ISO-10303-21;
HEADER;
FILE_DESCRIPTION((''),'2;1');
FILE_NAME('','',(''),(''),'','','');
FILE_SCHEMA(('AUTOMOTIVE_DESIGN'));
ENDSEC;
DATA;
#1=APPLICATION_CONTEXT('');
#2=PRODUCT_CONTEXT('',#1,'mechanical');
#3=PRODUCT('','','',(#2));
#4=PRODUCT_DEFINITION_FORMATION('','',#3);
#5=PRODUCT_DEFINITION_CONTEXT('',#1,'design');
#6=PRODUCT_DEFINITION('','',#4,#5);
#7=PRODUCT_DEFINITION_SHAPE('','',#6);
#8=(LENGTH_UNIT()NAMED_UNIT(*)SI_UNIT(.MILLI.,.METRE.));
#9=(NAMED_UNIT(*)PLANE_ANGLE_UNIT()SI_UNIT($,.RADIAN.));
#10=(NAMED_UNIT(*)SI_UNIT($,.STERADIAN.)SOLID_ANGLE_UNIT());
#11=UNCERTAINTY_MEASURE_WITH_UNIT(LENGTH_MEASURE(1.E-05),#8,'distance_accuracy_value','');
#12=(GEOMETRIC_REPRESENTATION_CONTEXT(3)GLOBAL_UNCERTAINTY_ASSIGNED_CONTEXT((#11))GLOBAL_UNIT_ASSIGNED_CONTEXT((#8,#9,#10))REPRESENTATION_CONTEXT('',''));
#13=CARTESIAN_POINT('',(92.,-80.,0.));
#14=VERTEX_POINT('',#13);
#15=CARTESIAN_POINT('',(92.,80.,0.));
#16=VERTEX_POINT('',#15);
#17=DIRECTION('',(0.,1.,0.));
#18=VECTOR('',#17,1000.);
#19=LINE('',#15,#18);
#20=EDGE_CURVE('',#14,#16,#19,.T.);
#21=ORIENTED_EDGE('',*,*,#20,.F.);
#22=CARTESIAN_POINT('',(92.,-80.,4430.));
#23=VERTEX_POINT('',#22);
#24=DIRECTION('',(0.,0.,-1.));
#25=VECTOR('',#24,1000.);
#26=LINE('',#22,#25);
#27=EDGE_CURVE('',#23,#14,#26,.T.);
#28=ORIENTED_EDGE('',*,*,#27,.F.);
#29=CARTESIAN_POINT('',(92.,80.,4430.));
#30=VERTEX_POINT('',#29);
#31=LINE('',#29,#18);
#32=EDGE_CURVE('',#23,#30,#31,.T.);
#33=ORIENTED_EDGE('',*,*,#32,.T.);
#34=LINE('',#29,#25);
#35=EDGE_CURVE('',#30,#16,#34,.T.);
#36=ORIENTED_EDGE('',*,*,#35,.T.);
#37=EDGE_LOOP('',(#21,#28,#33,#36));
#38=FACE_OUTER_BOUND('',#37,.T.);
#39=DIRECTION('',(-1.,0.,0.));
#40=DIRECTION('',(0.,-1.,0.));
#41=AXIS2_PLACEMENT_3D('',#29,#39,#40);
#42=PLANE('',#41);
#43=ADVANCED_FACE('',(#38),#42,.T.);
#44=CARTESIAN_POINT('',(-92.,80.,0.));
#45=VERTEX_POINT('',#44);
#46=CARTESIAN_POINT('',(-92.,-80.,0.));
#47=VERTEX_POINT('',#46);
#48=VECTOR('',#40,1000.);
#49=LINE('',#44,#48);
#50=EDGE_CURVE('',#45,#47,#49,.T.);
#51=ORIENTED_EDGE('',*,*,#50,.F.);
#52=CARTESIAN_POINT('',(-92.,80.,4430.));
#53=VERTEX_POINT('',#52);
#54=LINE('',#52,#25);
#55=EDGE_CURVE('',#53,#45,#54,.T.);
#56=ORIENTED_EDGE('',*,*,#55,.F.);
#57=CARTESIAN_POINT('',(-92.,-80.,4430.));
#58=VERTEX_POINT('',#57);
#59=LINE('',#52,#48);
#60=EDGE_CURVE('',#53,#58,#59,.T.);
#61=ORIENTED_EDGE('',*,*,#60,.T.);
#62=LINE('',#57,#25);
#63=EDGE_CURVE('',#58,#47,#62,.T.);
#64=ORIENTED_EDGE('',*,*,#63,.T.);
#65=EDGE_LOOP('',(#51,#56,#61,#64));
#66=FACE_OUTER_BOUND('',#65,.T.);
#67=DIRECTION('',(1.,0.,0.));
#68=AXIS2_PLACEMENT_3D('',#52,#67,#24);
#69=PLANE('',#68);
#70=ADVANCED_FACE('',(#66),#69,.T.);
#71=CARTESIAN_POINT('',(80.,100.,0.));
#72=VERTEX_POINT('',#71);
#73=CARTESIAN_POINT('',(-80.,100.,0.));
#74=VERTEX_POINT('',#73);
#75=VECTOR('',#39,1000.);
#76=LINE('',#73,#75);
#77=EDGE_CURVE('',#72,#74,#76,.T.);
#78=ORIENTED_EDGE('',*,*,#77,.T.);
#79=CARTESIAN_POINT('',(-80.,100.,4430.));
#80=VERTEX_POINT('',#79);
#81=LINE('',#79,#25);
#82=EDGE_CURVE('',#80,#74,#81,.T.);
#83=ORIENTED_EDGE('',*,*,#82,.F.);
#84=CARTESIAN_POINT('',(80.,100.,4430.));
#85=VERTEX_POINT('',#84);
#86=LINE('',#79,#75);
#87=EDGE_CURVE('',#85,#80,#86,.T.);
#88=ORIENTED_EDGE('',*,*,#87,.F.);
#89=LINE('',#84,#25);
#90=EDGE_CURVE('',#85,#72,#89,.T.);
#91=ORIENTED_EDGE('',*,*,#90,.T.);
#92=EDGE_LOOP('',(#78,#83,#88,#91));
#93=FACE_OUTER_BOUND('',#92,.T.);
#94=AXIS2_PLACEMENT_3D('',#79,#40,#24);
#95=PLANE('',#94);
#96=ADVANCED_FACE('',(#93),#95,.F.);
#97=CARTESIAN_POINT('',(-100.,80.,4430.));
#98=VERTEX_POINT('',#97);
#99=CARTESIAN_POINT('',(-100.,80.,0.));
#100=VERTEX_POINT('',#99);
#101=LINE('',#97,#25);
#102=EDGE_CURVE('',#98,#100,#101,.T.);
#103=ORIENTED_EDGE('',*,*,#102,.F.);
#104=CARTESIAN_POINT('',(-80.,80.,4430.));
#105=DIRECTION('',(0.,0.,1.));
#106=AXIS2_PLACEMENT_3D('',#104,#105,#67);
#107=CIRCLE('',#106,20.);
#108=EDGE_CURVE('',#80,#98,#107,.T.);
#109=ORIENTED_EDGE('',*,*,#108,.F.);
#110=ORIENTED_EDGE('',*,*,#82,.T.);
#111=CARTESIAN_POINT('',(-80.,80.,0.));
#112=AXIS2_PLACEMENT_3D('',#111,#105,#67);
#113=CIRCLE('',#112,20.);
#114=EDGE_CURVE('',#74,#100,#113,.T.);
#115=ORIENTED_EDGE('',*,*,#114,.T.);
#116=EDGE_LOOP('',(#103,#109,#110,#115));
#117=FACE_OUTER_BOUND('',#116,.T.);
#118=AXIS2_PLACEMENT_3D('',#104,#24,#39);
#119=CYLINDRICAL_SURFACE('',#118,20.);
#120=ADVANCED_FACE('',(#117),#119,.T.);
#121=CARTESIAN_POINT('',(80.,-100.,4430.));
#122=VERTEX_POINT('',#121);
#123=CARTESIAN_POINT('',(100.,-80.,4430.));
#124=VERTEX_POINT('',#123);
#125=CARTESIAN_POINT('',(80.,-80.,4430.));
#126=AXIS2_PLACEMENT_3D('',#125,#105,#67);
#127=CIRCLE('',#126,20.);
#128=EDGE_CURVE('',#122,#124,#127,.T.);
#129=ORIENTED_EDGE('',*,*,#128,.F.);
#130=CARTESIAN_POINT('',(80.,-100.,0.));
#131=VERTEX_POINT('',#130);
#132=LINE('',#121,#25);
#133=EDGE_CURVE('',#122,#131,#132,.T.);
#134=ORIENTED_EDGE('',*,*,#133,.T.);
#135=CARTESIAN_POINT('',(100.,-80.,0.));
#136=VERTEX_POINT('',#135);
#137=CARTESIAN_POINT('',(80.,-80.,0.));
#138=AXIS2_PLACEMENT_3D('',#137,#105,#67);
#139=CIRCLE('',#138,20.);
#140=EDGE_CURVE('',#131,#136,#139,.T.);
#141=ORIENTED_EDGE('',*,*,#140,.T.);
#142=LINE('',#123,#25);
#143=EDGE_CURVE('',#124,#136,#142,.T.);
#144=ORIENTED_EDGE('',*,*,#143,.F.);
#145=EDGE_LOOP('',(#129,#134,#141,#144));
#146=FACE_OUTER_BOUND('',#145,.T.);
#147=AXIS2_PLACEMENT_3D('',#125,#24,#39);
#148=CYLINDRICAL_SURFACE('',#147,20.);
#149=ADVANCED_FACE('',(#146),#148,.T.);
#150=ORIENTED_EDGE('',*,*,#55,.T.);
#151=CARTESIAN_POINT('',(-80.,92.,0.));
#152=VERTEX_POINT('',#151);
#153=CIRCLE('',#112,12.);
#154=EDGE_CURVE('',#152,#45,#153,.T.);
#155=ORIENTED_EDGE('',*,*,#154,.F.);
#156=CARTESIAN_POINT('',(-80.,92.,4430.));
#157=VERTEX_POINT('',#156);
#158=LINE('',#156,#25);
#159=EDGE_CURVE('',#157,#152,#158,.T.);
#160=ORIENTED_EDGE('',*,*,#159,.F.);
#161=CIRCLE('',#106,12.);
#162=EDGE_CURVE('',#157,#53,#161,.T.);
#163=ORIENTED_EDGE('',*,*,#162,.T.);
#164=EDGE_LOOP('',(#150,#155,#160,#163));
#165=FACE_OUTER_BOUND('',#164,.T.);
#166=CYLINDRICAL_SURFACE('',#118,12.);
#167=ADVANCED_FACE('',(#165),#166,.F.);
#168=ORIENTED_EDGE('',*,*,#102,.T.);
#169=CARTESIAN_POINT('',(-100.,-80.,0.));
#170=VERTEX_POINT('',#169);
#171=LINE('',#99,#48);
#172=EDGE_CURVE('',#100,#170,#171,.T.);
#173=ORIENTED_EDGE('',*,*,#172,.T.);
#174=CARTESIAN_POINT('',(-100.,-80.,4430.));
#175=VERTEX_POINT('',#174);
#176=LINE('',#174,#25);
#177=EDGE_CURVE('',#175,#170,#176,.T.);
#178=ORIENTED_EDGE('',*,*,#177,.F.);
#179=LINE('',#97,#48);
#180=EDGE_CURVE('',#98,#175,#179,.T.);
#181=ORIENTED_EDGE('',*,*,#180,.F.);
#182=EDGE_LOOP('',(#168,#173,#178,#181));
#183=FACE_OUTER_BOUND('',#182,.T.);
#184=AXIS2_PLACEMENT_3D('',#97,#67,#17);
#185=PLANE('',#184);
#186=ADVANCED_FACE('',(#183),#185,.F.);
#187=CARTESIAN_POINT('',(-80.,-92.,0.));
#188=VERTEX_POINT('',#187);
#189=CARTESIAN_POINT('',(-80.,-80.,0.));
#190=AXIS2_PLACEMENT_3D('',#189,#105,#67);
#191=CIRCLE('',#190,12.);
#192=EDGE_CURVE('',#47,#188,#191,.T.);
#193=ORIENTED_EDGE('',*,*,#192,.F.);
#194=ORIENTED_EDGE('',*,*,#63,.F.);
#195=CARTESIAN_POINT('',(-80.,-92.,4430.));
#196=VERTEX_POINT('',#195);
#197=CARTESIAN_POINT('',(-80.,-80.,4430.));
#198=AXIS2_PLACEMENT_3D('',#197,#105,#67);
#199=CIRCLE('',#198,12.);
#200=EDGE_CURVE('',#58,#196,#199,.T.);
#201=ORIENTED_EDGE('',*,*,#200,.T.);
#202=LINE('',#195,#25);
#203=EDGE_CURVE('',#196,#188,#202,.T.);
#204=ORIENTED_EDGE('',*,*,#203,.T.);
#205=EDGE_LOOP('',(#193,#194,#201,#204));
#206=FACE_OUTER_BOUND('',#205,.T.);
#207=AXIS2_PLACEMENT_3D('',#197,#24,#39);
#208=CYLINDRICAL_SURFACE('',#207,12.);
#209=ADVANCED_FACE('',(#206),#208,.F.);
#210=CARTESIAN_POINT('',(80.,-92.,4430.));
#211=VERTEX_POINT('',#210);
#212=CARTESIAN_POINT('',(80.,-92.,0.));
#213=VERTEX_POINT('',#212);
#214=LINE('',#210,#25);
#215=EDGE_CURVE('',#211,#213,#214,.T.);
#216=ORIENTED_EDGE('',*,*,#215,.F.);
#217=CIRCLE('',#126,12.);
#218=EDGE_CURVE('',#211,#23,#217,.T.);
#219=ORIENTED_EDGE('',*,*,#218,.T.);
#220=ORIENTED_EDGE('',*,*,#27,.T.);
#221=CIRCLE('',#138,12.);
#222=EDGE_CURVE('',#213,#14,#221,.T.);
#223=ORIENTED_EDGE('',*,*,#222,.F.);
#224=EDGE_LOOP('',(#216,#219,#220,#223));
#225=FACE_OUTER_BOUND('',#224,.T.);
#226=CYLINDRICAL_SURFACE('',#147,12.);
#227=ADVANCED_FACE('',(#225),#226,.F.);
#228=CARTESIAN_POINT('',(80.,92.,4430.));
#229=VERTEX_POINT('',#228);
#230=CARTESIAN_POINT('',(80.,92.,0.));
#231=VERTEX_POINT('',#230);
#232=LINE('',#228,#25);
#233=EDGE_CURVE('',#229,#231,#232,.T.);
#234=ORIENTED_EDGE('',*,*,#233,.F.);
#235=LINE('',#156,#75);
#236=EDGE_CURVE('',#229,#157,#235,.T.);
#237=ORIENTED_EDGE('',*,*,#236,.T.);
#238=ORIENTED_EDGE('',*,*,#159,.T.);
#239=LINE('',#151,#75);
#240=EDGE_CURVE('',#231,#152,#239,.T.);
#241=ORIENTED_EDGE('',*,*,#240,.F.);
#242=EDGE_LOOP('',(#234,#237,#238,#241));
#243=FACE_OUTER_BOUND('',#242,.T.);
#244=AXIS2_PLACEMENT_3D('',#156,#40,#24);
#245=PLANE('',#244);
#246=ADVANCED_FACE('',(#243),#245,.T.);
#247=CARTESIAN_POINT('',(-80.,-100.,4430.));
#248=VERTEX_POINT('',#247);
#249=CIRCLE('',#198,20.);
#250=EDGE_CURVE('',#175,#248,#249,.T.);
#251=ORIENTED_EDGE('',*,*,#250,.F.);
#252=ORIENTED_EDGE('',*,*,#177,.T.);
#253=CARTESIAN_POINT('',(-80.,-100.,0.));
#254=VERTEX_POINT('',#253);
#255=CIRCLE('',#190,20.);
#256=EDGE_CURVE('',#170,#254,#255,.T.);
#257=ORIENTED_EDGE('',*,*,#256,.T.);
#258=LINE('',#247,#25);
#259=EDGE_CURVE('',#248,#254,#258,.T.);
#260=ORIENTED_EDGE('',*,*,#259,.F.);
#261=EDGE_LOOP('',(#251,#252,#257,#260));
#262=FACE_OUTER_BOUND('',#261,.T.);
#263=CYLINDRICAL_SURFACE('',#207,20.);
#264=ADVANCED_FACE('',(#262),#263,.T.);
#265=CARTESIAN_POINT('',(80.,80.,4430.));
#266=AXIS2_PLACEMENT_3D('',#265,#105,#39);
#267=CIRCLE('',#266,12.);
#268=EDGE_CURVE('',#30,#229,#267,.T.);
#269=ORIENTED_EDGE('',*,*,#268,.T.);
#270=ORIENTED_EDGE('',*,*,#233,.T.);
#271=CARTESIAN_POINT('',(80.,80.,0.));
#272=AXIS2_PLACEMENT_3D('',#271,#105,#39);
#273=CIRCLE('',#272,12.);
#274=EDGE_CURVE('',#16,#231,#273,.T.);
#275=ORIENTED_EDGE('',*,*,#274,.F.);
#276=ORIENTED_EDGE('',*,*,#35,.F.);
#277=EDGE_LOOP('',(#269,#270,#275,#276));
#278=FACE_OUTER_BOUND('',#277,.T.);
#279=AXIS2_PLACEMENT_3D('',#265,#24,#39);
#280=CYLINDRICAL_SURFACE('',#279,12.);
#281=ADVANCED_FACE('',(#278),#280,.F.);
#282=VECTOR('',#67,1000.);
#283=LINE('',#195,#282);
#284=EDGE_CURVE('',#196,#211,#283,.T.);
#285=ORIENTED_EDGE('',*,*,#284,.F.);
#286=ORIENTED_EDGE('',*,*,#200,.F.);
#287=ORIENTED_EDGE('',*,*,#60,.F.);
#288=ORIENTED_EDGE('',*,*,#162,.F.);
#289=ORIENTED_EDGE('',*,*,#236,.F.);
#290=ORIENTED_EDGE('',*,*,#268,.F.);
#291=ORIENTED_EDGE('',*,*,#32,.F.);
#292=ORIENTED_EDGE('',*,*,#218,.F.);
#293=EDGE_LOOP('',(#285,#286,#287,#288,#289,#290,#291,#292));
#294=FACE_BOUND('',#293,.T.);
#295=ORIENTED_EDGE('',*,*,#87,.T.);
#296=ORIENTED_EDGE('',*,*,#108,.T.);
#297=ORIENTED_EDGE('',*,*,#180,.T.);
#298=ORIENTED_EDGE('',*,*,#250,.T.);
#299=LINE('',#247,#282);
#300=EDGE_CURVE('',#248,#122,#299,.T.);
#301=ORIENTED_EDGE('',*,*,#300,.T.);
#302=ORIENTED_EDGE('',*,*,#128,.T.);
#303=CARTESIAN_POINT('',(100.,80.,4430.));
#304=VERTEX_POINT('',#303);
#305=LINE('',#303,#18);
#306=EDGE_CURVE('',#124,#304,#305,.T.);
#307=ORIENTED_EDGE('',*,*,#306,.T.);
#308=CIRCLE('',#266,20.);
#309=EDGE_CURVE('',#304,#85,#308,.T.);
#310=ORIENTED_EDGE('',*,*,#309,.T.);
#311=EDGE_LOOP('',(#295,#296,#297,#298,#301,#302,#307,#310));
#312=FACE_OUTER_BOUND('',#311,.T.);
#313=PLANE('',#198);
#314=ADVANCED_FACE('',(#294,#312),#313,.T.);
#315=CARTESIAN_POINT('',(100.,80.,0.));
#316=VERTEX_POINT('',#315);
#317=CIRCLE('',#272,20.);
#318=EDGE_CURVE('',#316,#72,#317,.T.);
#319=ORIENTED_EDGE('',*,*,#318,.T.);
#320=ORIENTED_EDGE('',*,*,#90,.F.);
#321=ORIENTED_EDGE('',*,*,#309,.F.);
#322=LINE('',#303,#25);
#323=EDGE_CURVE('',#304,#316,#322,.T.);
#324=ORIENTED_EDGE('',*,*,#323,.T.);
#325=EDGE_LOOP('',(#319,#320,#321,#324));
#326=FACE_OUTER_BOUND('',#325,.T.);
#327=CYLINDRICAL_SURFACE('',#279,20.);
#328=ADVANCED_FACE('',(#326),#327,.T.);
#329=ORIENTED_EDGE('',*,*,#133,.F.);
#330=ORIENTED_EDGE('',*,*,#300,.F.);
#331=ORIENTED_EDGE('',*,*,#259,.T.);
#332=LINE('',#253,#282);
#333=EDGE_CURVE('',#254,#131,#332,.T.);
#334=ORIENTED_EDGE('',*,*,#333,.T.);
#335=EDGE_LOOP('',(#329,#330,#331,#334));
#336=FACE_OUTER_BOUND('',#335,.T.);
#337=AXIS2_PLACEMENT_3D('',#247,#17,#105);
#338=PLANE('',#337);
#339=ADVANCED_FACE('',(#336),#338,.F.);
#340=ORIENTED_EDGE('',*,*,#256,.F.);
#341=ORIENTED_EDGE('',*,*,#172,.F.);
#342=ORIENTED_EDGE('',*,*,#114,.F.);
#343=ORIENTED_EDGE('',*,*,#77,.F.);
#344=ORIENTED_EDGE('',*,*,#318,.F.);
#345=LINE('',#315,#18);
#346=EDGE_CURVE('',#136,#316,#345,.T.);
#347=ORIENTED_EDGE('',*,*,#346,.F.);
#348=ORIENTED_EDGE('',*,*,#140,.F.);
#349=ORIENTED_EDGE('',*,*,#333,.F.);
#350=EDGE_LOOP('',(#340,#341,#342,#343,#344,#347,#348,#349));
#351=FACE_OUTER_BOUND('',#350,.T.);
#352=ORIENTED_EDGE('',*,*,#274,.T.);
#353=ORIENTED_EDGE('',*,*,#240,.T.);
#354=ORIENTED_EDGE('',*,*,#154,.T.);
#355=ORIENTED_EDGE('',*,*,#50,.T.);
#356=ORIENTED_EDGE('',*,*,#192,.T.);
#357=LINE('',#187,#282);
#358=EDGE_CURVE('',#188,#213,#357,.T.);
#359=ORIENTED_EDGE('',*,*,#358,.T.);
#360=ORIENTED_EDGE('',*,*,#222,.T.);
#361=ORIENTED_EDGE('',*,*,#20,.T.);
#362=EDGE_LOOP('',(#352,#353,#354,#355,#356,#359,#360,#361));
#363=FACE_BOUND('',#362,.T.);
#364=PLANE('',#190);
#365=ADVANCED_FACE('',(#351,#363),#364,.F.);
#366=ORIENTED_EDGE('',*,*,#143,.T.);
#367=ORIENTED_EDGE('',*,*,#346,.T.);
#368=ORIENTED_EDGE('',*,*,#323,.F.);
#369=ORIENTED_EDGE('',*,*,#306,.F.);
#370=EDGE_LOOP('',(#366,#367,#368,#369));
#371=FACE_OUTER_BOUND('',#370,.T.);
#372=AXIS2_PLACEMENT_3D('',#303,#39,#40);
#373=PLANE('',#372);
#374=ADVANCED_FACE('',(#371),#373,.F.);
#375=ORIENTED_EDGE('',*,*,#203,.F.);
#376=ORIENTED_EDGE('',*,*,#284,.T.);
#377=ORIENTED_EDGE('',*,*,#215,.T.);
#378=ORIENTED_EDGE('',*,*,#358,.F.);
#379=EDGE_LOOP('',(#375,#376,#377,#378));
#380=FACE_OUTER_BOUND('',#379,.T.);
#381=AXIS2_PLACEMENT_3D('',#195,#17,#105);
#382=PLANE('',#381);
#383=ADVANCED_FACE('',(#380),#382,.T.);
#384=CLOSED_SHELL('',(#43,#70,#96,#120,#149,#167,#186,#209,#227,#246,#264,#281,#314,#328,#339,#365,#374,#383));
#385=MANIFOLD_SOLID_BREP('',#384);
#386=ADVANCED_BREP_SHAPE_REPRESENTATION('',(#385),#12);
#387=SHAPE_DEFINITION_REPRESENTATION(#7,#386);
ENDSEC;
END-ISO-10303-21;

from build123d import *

# Parameters (mm, degrees)
BOSS_EXTRUDE1_DEPTH = 4430


with BuildPart() as part:
    # Sketch1 → Boss-Extrude1 (new body)
    with BuildSketch(Plane.XY):
        with BuildLine():
            Line((-80, 100), (80, 100))
            ThreePointArc((80, 100), (94.142135624, 94.142135624), (100, 80))
            Line((100, 80), (100, -80))
            ThreePointArc((100, -80), (94.142135624, -94.142135624), (80, -100))
            Line((80, -100), (-80, -100))
            ThreePointArc((-80, -100), (-94.142135624, -94.142135624), (-100, -80))
            Line((-100, -80), (-100, 80))
            ThreePointArc((-100, 80), (-94.142135624, 94.142135624), (-80, 100))
        make_face()
        with BuildLine():
            Line((-92, 80), (-92, -80))
            ThreePointArc((-92, -80), (-88.485281374, -88.485281374), (-80, -92))
            Line((-80, -92), (80, -92))
            ThreePointArc((80, -92), (88.485281374, -88.485281374), (92, -80))
            Line((92, -80), (92, 80))
            ThreePointArc((92, 80), (88.485281374, 88.485281374), (80, 92))
            Line((80, 92), (-80, 92))
            ThreePointArc((-80, 92), (-88.485281374, 88.485281374), (-92, 80))
        make_face(mode=Mode.SUBTRACT)
    extrude(amount=BOSS_EXTRUDE1_DEPTH)


solid = part.part
